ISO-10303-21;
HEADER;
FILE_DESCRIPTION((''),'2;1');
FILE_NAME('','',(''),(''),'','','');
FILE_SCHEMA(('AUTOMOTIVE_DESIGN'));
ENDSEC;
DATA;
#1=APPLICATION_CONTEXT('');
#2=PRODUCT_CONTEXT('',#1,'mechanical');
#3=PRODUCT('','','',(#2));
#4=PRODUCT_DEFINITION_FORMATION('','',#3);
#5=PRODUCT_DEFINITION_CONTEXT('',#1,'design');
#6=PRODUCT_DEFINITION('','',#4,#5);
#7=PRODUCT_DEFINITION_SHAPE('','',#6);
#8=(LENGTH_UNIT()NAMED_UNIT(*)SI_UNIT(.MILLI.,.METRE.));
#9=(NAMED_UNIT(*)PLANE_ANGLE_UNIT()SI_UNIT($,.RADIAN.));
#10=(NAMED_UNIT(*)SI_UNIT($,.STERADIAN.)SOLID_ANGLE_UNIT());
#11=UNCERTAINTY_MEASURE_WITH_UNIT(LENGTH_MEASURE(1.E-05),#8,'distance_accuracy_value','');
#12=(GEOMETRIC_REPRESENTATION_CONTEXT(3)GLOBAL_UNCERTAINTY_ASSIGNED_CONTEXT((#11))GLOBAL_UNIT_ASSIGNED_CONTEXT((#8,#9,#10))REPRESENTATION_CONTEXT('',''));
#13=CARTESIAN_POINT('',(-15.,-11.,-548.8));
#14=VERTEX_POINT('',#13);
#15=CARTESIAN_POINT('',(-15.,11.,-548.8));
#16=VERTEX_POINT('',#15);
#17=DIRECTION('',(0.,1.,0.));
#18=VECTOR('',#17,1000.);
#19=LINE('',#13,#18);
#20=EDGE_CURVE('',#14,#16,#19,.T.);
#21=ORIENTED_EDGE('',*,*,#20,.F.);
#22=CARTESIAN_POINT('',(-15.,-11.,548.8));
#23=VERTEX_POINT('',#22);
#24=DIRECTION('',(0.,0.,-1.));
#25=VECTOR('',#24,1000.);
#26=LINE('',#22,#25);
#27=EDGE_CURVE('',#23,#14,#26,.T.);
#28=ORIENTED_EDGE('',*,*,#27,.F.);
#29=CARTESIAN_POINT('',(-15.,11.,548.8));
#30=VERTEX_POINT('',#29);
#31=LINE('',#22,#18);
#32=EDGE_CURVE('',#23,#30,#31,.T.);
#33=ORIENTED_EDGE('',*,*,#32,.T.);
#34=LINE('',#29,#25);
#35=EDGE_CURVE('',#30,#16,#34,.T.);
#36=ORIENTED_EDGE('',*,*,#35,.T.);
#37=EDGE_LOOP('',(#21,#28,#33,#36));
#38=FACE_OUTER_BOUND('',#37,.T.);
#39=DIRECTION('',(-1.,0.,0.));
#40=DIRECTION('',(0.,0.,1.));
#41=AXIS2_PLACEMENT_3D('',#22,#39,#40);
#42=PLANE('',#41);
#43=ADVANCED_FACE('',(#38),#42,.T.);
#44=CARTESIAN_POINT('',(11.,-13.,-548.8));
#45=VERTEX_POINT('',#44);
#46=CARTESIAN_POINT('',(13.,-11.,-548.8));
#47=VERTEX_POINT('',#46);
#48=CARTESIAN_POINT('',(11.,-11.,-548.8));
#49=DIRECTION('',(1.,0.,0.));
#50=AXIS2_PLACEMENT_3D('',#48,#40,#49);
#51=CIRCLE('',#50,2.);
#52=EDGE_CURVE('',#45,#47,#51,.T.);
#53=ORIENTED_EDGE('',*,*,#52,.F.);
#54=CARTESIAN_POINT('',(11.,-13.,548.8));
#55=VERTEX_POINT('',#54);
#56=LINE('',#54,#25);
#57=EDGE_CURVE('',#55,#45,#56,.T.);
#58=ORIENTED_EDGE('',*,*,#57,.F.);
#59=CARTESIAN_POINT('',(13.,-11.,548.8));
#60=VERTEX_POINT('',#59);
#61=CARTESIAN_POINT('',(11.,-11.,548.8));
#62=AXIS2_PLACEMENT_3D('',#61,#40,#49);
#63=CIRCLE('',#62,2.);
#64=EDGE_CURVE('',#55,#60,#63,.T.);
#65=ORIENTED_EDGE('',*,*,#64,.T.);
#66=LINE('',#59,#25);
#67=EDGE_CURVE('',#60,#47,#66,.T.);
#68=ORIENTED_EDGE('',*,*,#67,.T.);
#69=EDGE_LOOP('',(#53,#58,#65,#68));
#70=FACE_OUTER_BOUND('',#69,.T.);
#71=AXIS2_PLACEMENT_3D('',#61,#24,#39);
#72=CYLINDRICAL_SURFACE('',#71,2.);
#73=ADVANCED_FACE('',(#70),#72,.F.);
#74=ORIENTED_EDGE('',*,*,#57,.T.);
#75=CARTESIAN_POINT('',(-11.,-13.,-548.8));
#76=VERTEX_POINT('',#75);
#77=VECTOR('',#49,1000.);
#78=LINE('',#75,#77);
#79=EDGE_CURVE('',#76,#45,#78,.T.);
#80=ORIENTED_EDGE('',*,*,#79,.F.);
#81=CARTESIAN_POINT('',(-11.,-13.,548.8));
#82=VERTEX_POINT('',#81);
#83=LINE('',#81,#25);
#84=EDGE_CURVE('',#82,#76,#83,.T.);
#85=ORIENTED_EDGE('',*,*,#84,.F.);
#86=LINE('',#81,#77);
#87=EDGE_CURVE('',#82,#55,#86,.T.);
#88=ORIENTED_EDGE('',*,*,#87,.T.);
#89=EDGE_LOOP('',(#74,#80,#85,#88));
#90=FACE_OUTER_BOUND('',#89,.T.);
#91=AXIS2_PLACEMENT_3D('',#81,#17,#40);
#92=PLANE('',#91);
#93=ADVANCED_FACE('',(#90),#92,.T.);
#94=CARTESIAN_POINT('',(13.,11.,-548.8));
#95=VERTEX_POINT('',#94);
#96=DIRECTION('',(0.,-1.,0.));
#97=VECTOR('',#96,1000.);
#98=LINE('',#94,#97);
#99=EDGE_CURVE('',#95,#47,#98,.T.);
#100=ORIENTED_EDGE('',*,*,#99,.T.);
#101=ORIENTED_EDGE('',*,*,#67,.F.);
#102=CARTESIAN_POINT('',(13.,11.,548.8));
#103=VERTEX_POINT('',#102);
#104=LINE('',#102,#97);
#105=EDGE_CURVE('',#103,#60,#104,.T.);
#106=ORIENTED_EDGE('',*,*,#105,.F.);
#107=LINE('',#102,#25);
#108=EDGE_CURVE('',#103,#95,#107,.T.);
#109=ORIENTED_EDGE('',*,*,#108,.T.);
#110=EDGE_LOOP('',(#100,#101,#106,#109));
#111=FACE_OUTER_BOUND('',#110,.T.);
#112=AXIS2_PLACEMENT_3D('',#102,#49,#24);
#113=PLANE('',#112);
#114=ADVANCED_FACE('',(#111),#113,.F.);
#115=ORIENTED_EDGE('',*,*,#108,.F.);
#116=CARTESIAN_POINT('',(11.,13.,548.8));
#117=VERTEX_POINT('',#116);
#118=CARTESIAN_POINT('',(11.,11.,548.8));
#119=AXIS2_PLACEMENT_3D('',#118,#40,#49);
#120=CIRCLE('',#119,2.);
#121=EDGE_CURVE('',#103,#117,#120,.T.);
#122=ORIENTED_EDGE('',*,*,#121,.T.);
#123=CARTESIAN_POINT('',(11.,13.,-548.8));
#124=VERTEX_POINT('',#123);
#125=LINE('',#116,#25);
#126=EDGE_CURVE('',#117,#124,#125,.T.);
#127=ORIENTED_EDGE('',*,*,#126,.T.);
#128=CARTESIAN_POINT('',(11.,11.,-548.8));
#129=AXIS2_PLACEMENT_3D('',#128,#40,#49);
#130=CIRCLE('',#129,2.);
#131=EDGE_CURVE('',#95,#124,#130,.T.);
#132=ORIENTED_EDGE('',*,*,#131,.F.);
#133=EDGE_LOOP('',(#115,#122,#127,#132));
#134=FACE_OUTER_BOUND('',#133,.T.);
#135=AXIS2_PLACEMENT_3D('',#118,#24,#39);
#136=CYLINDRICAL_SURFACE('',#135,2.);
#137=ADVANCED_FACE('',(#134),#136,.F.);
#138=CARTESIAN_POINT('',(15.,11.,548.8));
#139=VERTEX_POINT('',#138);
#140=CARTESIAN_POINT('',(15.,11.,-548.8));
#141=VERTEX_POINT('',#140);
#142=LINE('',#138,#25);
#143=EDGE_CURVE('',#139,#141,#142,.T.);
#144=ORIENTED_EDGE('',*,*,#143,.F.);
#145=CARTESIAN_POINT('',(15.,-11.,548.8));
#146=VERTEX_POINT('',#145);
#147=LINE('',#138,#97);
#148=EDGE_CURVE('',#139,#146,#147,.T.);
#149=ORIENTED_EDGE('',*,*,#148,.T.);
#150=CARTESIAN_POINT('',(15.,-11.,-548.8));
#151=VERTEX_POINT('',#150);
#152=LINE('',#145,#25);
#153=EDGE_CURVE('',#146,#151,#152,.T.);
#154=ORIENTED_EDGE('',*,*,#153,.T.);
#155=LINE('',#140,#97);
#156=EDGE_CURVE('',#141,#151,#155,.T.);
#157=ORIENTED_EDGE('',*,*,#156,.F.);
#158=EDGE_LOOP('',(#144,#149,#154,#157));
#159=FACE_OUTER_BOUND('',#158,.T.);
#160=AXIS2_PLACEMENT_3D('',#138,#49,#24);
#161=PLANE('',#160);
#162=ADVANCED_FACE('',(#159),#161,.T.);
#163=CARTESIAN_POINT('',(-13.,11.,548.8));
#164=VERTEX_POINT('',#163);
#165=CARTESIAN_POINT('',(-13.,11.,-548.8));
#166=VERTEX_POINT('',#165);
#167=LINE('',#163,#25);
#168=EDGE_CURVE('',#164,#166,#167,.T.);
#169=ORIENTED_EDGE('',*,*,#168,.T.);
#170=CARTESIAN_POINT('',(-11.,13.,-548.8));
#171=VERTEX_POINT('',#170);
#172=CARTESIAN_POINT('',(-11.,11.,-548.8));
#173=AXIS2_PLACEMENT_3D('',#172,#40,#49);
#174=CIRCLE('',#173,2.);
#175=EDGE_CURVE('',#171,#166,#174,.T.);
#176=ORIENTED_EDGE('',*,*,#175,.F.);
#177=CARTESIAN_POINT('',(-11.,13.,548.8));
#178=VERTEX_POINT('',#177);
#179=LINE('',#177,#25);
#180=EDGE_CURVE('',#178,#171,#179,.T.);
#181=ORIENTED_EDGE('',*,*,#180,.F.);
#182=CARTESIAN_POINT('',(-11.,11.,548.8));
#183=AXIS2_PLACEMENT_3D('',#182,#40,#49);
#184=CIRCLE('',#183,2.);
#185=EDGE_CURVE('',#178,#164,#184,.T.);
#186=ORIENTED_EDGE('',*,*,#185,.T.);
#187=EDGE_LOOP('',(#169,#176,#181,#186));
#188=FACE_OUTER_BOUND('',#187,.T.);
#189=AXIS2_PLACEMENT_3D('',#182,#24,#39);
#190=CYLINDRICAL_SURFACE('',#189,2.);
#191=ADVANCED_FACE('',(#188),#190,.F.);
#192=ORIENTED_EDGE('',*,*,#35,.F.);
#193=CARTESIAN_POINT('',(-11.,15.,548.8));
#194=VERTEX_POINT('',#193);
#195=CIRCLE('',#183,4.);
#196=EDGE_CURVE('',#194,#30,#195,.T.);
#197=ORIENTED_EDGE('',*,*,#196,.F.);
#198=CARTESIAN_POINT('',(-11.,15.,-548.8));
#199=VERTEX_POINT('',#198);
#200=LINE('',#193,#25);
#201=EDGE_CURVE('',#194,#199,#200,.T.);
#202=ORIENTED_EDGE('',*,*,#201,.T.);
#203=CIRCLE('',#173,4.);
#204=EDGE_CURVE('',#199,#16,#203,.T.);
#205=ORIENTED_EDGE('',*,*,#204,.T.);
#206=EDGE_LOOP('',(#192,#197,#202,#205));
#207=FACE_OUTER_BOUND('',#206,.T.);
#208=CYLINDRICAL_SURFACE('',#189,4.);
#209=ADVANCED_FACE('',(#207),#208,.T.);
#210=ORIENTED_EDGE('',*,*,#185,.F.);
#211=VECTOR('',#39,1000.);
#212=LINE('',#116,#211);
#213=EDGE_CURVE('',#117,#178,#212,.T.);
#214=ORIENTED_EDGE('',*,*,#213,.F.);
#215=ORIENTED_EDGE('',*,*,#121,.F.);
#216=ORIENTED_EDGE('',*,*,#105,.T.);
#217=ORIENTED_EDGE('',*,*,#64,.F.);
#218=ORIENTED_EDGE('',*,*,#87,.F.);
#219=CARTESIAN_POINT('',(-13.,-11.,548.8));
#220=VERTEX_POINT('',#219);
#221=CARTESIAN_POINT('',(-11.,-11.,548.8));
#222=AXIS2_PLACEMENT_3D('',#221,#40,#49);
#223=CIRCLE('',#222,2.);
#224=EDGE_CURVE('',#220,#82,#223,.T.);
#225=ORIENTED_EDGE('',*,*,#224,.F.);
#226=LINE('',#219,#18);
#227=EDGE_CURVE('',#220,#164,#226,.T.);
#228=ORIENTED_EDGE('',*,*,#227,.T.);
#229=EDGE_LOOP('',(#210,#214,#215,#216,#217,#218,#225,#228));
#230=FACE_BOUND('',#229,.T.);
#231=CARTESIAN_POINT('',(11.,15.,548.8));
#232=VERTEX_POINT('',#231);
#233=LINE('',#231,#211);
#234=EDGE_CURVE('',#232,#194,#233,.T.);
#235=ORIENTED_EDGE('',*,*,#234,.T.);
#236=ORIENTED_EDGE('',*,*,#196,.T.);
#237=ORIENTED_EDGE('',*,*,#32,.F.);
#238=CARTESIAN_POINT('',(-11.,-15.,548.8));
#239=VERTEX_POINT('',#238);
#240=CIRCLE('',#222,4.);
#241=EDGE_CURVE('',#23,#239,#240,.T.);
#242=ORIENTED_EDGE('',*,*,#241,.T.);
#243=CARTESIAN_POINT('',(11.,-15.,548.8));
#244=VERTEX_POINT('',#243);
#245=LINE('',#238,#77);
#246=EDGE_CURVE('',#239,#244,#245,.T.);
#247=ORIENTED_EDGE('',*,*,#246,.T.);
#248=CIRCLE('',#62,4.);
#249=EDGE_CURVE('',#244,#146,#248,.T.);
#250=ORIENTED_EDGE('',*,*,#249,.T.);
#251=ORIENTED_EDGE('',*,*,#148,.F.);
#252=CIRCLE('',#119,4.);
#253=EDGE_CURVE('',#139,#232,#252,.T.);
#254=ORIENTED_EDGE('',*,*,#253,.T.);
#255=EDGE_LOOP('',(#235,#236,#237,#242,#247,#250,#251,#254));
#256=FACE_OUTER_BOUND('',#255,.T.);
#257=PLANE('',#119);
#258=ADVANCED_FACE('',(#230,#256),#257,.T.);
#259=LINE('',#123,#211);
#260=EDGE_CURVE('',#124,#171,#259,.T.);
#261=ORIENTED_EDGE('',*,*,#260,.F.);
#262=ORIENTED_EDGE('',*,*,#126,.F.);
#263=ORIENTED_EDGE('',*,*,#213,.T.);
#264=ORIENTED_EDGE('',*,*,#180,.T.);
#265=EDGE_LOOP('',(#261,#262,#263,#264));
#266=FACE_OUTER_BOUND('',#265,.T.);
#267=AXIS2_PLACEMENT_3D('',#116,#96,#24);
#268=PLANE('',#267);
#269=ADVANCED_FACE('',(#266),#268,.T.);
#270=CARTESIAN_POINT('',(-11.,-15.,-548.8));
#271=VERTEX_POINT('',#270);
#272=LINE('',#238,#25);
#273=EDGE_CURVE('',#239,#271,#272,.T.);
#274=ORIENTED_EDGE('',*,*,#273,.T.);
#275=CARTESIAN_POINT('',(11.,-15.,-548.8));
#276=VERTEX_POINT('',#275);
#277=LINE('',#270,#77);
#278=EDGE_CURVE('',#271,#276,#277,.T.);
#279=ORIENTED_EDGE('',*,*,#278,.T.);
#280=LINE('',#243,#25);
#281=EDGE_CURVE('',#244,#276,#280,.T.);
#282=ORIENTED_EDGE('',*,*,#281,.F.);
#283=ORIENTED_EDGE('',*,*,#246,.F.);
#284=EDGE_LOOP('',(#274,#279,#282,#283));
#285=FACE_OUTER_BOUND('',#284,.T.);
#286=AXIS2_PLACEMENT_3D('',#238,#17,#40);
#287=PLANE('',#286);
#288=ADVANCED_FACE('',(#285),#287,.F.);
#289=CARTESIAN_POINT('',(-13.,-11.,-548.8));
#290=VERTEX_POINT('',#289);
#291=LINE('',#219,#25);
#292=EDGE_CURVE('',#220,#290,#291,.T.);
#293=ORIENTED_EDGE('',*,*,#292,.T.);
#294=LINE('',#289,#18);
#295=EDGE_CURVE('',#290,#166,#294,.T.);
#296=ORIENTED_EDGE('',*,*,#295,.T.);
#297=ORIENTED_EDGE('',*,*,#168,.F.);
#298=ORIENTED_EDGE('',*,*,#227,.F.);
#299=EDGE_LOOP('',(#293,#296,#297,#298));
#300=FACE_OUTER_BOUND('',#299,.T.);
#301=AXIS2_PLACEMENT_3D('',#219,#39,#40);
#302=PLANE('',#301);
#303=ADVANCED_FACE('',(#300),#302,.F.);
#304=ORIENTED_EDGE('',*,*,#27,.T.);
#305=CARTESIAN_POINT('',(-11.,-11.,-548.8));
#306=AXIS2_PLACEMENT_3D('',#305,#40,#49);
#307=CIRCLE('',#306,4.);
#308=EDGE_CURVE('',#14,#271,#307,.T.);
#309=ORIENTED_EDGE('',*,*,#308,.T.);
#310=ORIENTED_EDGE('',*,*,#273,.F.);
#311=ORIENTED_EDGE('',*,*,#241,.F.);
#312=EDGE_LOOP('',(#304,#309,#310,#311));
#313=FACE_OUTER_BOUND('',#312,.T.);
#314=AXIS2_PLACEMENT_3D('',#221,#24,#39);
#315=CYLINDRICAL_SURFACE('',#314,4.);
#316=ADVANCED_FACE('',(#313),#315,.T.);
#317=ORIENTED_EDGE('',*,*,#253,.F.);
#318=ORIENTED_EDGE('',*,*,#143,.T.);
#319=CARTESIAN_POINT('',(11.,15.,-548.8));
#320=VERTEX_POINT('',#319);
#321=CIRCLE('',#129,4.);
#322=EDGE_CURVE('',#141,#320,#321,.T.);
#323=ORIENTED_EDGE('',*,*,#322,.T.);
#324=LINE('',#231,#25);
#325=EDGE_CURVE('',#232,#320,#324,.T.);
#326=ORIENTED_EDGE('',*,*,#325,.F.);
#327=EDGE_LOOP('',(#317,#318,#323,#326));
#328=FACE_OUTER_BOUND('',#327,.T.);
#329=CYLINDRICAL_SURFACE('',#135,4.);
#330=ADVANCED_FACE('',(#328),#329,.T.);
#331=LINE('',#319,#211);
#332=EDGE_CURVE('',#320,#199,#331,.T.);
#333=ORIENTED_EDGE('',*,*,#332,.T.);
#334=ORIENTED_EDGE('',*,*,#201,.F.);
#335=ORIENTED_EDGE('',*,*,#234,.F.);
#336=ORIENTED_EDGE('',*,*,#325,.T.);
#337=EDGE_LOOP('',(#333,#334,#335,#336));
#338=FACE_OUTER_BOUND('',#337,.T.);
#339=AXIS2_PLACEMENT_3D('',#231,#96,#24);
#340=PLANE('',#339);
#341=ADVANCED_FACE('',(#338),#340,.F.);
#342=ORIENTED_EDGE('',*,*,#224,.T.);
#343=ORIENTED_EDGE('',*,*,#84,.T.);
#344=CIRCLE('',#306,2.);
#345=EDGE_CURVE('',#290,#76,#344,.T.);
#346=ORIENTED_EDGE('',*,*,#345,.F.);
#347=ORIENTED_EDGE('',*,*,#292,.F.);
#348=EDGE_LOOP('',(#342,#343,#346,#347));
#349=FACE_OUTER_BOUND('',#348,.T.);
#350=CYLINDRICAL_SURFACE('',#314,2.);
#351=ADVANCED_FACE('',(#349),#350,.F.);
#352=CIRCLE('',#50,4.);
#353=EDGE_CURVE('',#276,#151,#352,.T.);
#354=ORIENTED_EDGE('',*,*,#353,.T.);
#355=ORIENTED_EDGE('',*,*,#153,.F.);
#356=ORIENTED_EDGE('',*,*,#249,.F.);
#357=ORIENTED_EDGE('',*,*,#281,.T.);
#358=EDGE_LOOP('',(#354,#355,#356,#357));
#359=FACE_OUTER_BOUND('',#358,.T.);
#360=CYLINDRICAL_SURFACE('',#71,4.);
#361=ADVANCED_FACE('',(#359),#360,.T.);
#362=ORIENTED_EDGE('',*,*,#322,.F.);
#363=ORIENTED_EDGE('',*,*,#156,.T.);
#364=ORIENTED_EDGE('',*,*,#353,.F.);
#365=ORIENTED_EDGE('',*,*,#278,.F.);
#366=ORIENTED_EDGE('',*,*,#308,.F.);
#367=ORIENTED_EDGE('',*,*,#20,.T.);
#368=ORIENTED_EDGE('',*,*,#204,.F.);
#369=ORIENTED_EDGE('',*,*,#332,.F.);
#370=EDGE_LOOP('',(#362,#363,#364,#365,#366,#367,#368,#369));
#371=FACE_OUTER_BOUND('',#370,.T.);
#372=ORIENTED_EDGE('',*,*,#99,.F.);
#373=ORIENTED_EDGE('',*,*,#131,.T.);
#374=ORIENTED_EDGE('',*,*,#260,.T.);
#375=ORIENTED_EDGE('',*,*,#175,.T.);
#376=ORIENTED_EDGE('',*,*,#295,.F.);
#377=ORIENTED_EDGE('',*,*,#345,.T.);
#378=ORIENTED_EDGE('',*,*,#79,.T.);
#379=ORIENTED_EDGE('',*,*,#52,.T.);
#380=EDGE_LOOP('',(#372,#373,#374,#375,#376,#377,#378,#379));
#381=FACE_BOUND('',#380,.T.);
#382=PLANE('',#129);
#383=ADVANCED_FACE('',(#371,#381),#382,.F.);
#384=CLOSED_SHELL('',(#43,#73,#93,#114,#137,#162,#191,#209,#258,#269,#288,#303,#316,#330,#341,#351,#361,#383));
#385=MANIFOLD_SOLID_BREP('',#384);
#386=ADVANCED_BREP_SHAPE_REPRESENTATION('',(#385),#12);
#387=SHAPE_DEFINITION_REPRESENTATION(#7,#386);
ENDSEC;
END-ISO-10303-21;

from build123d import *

# Parameters (mm, degrees)
EXTRUDE_THIN1_DEPTH = 548.8


with BuildPart() as part:
    # Sketch1 → Extrude-Thin1 (new, symmetric)
    with BuildSketch(Plane.XY):
        with BuildLine():
            Line((-15, 11), (-15, -11))
            ThreePointArc((-15, -11), (-13.828427125, -13.828427125), (-11, -15))
            Line((-11, -15), (11, -15))
            ThreePointArc((11, -15), (13.828427125, -13.828427125), (15, -11))
            Line((15, -11), (15, 11))
            ThreePointArc((15, 11), (13.828427125, 13.828427125), (11, 15))
            Line((11, 15), (-11, 15))
            ThreePointArc((-11, 15), (-13.828427125, 13.828427125), (-15, 11))
        make_face()
        with BuildLine():
            Line((-13, 11), (-13, -11))
            ThreePointArc((-13, -11), (-12.414213562, -12.414213562), (-11, -13))
            Line((-11, -13), (11, -13))
            ThreePointArc((11, -13), (12.414213562, -12.414213562), (13, -11))
            Line((13, -11), (13, 11))
            ThreePointArc((13, 11), (12.414213562, 12.414213562), (11, 13))
            Line((11, 13), (-11, 13))
            ThreePointArc((-11, 13), (-12.414213562, 12.414213562), (-13, 11))
        make_face(mode=Mode.SUBTRACT)
    extrude(amount=EXTRUDE_THIN1_DEPTH, both=True)


solid = part.part
